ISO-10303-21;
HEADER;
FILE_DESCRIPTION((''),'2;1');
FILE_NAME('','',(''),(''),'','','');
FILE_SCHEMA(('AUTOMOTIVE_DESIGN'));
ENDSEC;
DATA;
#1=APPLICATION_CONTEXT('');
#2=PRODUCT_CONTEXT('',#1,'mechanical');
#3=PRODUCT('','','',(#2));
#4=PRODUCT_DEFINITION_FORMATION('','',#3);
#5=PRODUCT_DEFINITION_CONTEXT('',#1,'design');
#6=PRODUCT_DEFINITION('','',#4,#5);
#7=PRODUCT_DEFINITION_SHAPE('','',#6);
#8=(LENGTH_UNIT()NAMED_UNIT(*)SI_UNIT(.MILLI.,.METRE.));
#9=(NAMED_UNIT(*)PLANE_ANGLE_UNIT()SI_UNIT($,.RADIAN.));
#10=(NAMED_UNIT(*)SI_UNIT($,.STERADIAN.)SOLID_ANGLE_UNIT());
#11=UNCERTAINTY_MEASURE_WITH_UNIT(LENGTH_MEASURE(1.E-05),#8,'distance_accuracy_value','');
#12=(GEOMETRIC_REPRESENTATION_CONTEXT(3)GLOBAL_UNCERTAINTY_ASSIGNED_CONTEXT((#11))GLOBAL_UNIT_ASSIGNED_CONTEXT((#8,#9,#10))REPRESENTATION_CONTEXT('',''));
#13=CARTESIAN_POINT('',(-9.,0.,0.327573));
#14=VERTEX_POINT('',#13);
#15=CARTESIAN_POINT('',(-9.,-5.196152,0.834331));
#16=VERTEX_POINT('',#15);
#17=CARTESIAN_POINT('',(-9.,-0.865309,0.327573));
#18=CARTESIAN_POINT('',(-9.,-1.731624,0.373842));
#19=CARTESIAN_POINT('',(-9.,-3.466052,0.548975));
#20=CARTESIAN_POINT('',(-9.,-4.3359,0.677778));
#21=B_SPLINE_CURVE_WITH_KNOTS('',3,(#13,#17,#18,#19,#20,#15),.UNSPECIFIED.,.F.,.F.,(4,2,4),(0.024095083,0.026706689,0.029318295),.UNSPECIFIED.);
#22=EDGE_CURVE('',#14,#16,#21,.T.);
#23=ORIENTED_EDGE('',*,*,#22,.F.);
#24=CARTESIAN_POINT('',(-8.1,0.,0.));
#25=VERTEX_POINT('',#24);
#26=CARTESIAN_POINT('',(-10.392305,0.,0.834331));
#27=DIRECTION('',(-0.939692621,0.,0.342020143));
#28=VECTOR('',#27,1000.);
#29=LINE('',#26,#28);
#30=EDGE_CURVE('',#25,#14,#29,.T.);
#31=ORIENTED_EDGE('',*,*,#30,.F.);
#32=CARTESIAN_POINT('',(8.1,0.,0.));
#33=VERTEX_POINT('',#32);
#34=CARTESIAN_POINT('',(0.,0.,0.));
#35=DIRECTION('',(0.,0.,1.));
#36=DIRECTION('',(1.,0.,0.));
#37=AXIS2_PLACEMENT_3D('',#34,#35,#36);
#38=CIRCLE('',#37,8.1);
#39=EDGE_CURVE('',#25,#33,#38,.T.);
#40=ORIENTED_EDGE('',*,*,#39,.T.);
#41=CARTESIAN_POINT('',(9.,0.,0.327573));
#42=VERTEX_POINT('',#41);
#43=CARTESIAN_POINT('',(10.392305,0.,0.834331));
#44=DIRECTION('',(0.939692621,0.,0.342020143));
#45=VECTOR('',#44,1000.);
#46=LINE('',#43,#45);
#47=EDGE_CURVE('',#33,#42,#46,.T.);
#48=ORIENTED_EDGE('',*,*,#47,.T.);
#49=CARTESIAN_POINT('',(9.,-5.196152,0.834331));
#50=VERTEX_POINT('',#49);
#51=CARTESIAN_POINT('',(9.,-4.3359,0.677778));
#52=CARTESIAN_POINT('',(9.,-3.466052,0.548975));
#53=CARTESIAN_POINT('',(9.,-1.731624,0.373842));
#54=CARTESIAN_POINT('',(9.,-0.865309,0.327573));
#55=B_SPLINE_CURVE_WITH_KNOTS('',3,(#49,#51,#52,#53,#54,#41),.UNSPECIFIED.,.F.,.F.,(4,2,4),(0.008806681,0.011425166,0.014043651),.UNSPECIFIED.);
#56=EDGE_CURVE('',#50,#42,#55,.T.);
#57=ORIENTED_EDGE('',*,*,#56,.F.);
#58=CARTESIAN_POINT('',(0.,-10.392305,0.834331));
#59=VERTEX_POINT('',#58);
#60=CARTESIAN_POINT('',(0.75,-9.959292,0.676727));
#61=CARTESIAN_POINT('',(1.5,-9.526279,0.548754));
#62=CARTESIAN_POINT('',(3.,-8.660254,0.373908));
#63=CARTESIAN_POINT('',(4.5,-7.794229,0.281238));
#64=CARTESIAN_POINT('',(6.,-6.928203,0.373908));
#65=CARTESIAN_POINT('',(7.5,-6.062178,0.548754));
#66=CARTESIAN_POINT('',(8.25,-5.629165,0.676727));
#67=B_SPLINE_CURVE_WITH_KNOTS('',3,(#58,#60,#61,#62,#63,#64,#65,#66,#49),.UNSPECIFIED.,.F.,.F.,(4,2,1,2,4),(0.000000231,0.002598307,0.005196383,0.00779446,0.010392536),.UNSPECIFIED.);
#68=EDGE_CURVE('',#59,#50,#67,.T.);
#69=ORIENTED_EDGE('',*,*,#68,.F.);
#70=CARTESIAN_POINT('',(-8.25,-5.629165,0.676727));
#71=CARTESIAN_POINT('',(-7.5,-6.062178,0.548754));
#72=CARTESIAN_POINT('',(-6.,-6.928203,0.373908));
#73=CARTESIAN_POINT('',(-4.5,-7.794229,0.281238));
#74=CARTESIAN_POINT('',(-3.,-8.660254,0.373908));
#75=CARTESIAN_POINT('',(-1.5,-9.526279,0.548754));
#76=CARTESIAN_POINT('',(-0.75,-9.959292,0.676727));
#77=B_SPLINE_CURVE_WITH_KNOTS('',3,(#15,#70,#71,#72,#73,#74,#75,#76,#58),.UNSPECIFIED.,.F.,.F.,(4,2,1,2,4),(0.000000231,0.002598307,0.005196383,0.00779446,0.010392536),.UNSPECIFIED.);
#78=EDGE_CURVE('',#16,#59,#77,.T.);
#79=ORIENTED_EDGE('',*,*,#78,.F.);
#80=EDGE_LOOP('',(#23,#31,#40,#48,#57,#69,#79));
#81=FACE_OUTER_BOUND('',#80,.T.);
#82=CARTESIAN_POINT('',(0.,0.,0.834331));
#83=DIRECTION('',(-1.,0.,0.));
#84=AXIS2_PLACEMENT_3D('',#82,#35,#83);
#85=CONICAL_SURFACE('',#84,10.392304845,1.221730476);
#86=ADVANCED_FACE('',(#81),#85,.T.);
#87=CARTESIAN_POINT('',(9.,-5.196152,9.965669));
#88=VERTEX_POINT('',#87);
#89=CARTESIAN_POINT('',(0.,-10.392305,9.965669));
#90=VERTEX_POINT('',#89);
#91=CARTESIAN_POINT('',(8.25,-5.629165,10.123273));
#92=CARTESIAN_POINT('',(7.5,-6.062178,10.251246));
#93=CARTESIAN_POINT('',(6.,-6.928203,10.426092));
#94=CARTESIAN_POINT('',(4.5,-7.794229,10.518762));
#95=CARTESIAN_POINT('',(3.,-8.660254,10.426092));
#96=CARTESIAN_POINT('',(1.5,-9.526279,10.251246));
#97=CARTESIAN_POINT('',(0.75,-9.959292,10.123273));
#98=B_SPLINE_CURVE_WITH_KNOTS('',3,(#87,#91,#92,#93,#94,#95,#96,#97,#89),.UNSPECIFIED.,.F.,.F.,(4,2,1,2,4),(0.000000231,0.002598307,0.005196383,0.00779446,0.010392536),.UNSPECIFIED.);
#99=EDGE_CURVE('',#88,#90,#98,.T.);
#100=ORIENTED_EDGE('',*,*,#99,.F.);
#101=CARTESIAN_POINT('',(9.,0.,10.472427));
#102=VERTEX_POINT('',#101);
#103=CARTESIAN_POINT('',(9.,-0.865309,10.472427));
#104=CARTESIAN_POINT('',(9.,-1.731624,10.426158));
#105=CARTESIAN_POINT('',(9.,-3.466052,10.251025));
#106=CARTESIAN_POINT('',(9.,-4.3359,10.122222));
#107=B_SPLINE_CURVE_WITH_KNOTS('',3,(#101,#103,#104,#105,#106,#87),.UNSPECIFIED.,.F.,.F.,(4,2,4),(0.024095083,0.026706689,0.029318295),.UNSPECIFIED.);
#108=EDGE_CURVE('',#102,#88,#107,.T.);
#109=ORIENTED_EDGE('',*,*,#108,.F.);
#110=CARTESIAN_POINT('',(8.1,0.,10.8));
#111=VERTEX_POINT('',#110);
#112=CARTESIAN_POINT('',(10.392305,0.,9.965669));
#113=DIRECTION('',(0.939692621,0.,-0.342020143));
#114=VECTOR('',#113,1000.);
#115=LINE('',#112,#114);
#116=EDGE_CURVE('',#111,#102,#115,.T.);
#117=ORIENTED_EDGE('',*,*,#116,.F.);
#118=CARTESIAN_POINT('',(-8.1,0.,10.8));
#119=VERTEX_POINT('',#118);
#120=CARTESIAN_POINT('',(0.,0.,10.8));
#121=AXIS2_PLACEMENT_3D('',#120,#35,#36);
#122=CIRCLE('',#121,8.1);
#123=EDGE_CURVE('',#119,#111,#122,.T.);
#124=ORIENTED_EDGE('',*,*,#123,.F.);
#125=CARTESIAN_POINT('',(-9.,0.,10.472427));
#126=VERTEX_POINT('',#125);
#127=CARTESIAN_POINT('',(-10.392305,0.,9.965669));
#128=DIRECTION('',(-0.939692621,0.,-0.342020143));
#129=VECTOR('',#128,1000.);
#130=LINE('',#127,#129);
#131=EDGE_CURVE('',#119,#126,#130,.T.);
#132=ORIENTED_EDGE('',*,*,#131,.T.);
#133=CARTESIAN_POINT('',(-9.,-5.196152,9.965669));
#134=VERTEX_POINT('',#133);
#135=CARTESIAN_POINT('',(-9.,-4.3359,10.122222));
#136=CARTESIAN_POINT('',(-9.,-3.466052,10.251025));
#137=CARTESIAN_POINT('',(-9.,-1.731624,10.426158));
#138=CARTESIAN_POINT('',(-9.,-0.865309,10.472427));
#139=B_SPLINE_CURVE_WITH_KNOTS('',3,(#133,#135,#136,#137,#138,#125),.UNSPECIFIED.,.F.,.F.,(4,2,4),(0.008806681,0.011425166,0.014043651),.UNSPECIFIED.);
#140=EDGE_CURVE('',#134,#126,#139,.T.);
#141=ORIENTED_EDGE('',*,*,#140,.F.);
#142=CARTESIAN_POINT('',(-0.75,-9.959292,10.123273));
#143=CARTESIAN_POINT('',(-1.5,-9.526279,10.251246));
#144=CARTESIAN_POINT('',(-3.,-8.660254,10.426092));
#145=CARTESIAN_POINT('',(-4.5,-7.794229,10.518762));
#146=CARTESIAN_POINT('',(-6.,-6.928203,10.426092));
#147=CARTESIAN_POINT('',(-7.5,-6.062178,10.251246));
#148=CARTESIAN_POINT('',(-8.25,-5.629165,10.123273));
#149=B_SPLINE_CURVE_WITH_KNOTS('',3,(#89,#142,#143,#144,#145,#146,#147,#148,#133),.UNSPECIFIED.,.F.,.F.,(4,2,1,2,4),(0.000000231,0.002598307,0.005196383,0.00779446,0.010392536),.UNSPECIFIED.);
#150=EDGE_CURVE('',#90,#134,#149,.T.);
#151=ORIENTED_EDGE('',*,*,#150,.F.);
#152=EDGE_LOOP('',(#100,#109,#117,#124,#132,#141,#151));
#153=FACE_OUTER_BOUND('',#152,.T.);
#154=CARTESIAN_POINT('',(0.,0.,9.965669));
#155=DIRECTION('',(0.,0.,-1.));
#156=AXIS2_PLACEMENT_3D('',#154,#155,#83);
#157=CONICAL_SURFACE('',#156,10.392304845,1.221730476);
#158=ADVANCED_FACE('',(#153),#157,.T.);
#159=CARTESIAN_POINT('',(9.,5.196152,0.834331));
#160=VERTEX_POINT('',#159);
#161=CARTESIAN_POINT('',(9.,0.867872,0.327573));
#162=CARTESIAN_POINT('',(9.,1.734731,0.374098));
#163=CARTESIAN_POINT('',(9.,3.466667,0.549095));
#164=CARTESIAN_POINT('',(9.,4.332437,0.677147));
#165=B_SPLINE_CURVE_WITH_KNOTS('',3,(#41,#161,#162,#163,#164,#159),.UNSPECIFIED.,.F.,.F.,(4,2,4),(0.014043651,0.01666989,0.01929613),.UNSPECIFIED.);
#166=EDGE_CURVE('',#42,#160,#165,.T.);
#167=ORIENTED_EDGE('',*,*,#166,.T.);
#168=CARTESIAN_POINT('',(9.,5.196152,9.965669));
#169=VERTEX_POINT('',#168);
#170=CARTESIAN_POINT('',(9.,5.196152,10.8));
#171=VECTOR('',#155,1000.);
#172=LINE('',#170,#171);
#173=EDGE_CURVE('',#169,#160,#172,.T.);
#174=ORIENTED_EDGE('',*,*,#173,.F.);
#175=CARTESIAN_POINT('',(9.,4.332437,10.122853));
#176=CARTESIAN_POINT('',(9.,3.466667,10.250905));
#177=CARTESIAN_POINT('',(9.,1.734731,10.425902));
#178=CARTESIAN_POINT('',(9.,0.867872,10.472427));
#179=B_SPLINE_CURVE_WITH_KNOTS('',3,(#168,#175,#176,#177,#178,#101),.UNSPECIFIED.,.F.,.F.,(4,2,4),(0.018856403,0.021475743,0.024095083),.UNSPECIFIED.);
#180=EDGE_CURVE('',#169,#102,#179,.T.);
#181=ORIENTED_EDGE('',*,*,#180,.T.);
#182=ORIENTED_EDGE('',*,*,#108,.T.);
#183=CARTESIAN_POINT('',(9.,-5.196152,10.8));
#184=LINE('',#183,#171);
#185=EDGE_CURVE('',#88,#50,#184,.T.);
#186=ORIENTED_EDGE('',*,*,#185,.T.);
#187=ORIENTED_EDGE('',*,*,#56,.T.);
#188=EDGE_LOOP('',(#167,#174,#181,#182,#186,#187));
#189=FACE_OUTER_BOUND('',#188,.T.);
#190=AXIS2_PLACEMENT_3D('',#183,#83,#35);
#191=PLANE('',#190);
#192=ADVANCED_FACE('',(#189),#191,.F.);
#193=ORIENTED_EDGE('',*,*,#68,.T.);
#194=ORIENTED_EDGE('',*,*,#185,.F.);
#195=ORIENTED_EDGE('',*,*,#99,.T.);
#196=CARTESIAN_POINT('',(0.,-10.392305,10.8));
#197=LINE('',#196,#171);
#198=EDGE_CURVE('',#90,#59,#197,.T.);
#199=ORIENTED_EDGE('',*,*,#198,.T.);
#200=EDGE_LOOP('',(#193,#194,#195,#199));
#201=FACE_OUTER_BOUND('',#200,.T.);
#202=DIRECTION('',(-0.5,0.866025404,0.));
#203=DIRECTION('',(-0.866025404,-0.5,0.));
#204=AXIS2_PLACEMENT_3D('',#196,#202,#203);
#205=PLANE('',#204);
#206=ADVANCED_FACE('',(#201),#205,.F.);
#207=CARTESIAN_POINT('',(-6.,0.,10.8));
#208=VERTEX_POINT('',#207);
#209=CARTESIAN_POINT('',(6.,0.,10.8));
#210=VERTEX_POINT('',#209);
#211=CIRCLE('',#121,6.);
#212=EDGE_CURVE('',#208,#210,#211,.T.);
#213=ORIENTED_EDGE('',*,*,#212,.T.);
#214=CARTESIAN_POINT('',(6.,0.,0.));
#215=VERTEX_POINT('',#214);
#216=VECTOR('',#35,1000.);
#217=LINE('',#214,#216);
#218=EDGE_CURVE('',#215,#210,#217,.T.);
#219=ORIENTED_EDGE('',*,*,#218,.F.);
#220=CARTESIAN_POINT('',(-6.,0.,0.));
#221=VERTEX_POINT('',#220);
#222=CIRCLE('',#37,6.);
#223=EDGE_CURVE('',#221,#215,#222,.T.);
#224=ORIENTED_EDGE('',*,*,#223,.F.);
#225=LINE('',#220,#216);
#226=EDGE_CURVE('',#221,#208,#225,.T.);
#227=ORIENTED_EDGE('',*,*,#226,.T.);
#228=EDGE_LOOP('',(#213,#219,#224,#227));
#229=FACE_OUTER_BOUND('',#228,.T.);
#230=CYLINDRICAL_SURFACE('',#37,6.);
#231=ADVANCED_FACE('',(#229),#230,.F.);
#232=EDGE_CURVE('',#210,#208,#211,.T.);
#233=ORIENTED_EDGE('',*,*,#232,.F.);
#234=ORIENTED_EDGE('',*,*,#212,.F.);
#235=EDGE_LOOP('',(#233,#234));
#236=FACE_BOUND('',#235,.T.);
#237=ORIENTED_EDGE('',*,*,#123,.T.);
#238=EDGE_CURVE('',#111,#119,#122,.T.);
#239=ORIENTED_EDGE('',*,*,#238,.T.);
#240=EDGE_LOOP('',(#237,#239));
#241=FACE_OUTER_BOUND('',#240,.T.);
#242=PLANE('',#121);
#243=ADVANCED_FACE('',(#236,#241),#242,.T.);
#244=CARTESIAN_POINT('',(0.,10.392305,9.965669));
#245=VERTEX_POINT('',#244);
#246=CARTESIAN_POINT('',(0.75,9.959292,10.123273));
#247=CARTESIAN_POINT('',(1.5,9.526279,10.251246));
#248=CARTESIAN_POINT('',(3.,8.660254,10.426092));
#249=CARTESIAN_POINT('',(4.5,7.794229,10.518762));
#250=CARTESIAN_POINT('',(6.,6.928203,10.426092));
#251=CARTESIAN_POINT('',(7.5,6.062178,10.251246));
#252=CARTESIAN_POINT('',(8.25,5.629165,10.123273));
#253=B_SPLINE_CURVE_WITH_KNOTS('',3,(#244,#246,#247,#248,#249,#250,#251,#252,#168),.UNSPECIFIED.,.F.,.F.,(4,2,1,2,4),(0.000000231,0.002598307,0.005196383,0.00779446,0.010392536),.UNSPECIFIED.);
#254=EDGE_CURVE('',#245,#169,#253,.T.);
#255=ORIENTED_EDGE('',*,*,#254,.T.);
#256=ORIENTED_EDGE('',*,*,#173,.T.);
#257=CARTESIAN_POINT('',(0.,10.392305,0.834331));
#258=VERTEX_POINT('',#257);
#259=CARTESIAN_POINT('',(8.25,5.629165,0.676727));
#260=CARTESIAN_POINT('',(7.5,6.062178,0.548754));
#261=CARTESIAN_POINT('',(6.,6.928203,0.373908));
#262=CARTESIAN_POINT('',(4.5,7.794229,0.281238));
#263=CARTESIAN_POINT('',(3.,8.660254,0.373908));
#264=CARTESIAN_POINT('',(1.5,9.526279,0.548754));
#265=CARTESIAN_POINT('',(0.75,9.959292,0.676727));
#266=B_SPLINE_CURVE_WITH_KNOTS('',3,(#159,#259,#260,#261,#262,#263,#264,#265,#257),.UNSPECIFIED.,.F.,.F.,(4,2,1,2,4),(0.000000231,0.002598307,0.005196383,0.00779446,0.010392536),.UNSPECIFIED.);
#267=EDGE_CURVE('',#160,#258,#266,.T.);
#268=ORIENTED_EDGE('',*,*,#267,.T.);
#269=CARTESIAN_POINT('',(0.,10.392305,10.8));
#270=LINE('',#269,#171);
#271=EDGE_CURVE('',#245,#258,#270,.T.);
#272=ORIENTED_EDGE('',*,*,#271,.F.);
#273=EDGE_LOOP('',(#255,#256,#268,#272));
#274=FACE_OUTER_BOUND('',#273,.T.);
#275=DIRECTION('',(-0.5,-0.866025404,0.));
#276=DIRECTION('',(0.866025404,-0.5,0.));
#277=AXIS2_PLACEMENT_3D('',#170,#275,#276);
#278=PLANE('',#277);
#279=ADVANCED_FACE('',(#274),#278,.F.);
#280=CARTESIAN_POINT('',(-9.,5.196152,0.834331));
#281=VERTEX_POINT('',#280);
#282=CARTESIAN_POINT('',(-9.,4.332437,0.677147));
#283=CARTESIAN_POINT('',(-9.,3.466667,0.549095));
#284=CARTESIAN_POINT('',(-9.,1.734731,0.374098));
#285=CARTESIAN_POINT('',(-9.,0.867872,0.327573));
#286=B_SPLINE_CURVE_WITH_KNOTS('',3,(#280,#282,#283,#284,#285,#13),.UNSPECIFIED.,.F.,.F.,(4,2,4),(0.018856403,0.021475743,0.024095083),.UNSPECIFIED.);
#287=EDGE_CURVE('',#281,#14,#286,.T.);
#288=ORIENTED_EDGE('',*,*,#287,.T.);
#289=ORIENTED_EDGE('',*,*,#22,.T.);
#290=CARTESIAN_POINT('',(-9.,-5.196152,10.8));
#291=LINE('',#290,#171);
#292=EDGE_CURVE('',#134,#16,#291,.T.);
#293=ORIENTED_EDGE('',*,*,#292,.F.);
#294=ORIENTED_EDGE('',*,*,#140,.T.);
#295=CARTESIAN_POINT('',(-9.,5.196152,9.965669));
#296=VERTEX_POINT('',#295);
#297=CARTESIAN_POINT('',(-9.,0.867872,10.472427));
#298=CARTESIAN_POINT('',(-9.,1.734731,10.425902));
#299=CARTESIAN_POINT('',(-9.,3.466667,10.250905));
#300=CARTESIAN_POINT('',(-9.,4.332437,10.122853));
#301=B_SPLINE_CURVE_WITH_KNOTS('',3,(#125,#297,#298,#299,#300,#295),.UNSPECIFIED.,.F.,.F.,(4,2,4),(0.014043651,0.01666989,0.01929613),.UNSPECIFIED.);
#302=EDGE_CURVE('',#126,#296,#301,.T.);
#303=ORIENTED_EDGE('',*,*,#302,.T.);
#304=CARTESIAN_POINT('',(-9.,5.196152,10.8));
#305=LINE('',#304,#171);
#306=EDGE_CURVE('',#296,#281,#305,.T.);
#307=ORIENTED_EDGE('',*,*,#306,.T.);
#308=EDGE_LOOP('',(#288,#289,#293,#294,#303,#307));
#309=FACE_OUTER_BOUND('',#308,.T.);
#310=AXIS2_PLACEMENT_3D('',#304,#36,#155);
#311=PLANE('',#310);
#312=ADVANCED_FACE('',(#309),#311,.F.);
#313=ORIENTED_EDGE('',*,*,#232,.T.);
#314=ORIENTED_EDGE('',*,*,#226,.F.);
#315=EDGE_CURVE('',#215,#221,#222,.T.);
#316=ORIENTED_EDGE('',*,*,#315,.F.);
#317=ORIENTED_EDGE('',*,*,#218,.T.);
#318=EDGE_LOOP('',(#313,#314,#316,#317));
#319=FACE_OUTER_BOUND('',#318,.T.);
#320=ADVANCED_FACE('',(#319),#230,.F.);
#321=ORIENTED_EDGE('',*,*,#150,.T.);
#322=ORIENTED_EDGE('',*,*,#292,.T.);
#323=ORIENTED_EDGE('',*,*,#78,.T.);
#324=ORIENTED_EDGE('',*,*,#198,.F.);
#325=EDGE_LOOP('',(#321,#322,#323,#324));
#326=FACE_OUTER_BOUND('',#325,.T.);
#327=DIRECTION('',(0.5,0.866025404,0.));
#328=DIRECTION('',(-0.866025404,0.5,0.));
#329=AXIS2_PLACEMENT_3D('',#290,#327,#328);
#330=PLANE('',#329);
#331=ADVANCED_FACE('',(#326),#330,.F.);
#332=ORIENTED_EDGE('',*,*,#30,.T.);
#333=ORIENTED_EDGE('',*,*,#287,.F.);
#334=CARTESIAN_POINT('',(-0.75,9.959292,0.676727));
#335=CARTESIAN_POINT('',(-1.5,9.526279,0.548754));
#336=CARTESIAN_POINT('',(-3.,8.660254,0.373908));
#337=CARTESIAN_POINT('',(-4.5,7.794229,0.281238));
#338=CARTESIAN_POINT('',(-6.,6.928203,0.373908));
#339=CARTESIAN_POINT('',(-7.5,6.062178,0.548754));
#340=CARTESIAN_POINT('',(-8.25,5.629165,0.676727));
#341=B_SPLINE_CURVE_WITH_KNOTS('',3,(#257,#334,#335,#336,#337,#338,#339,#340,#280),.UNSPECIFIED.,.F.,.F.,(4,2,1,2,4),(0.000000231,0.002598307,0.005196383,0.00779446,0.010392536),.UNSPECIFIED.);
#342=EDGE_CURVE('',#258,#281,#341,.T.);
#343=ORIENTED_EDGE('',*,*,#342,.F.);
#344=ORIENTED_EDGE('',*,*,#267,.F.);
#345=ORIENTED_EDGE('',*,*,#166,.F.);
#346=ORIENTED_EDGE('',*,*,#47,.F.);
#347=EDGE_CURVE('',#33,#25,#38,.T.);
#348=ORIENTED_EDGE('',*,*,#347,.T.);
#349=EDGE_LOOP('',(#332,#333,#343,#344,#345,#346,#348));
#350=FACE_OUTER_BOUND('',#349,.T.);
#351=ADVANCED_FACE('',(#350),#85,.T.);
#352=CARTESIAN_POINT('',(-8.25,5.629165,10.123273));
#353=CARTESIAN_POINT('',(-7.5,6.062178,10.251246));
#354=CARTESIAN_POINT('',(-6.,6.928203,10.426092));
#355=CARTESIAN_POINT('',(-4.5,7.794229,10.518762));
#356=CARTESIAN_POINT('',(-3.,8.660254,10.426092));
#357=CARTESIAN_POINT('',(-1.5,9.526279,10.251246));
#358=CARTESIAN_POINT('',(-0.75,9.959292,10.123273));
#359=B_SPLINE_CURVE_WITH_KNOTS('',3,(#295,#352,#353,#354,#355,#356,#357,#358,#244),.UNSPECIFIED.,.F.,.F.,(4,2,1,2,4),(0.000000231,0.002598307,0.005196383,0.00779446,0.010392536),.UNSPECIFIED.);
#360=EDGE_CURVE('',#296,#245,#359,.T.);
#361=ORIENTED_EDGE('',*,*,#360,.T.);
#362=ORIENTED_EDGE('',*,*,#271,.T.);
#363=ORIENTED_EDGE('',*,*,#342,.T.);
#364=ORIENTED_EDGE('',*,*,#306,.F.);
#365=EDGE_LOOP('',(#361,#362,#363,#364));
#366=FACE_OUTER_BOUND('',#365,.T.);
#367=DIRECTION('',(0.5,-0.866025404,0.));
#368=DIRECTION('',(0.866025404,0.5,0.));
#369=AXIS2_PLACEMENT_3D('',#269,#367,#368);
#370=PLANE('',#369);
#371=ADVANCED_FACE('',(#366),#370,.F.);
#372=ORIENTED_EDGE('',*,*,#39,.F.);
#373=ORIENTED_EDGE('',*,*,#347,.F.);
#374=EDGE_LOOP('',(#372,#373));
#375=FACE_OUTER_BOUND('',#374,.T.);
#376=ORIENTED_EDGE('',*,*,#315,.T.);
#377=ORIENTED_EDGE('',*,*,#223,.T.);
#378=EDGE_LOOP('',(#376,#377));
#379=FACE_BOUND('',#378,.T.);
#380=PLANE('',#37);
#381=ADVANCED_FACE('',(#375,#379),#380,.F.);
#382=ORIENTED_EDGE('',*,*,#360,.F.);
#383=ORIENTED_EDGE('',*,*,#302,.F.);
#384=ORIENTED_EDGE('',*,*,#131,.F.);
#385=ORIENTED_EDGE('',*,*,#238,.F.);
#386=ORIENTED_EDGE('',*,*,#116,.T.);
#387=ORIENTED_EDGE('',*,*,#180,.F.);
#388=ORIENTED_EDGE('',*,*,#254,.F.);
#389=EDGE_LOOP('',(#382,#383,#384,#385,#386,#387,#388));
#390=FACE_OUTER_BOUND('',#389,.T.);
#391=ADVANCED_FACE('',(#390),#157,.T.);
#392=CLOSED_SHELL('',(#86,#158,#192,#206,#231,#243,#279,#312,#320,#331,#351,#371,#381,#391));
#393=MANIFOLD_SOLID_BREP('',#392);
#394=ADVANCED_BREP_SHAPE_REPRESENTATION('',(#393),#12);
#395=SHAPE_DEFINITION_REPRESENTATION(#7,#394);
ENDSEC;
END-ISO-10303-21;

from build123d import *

# Parameters (mm, degrees)
BOSS_EXTRUDE1_DEPTH = 10.8
SKETCH5_R           = 6
CUT_EXTRUDE1_DEPTH  = 18.482562742


with BuildPart() as part:
    # Sketch1 → Boss-Extrude1 (new body)
    with BuildSketch(Plane.XY):
        Polygon((0, 10.392304845), (-9, 5.196152423), (-9, -5.196152423), (0, -10.392304845), (9, -5.196152423), (9, 5.196152423), align=None)
    extrude(amount=BOSS_EXTRUDE1_DEPTH)

    # Sketch4 → Cut-Revolve1 (revolve, cut)
    with BuildSketch(Plane(origin=(0, 0, 0), x_dir=(0, 0, -1), z_dir=(1, 0, 0)), mode=Mode.PRIVATE) as cut_revolve1_sk:
        Polygon((-10.8, -8.1), (-9.965669268, -10.392304845), (-10.8, -10.392304845), align=None)
    cut_revolve1 = revolve(cut_revolve1_sk.sketch.rotate(Axis((0, 0, 10.8), (0, 0, -1)), 119.999999988), axis=Axis((0, 0, 10.8), (0, 0, -1)), mode=Mode.SUBTRACT)

    # Mirror1: Cut-Revolve1 across plane
    add(cut_revolve1.mirror(Plane.XY.offset(5.4)), mode=Mode.SUBTRACT)

    # Sketch5 → Cut-Extrude1 (cut, through all)
    with BuildSketch(Plane.XY.offset(10.8)):
        Circle(SKETCH5_R)
    extrude(amount=-CUT_EXTRUDE1_DEPTH, mode=Mode.SUBTRACT)


solid = part.part
